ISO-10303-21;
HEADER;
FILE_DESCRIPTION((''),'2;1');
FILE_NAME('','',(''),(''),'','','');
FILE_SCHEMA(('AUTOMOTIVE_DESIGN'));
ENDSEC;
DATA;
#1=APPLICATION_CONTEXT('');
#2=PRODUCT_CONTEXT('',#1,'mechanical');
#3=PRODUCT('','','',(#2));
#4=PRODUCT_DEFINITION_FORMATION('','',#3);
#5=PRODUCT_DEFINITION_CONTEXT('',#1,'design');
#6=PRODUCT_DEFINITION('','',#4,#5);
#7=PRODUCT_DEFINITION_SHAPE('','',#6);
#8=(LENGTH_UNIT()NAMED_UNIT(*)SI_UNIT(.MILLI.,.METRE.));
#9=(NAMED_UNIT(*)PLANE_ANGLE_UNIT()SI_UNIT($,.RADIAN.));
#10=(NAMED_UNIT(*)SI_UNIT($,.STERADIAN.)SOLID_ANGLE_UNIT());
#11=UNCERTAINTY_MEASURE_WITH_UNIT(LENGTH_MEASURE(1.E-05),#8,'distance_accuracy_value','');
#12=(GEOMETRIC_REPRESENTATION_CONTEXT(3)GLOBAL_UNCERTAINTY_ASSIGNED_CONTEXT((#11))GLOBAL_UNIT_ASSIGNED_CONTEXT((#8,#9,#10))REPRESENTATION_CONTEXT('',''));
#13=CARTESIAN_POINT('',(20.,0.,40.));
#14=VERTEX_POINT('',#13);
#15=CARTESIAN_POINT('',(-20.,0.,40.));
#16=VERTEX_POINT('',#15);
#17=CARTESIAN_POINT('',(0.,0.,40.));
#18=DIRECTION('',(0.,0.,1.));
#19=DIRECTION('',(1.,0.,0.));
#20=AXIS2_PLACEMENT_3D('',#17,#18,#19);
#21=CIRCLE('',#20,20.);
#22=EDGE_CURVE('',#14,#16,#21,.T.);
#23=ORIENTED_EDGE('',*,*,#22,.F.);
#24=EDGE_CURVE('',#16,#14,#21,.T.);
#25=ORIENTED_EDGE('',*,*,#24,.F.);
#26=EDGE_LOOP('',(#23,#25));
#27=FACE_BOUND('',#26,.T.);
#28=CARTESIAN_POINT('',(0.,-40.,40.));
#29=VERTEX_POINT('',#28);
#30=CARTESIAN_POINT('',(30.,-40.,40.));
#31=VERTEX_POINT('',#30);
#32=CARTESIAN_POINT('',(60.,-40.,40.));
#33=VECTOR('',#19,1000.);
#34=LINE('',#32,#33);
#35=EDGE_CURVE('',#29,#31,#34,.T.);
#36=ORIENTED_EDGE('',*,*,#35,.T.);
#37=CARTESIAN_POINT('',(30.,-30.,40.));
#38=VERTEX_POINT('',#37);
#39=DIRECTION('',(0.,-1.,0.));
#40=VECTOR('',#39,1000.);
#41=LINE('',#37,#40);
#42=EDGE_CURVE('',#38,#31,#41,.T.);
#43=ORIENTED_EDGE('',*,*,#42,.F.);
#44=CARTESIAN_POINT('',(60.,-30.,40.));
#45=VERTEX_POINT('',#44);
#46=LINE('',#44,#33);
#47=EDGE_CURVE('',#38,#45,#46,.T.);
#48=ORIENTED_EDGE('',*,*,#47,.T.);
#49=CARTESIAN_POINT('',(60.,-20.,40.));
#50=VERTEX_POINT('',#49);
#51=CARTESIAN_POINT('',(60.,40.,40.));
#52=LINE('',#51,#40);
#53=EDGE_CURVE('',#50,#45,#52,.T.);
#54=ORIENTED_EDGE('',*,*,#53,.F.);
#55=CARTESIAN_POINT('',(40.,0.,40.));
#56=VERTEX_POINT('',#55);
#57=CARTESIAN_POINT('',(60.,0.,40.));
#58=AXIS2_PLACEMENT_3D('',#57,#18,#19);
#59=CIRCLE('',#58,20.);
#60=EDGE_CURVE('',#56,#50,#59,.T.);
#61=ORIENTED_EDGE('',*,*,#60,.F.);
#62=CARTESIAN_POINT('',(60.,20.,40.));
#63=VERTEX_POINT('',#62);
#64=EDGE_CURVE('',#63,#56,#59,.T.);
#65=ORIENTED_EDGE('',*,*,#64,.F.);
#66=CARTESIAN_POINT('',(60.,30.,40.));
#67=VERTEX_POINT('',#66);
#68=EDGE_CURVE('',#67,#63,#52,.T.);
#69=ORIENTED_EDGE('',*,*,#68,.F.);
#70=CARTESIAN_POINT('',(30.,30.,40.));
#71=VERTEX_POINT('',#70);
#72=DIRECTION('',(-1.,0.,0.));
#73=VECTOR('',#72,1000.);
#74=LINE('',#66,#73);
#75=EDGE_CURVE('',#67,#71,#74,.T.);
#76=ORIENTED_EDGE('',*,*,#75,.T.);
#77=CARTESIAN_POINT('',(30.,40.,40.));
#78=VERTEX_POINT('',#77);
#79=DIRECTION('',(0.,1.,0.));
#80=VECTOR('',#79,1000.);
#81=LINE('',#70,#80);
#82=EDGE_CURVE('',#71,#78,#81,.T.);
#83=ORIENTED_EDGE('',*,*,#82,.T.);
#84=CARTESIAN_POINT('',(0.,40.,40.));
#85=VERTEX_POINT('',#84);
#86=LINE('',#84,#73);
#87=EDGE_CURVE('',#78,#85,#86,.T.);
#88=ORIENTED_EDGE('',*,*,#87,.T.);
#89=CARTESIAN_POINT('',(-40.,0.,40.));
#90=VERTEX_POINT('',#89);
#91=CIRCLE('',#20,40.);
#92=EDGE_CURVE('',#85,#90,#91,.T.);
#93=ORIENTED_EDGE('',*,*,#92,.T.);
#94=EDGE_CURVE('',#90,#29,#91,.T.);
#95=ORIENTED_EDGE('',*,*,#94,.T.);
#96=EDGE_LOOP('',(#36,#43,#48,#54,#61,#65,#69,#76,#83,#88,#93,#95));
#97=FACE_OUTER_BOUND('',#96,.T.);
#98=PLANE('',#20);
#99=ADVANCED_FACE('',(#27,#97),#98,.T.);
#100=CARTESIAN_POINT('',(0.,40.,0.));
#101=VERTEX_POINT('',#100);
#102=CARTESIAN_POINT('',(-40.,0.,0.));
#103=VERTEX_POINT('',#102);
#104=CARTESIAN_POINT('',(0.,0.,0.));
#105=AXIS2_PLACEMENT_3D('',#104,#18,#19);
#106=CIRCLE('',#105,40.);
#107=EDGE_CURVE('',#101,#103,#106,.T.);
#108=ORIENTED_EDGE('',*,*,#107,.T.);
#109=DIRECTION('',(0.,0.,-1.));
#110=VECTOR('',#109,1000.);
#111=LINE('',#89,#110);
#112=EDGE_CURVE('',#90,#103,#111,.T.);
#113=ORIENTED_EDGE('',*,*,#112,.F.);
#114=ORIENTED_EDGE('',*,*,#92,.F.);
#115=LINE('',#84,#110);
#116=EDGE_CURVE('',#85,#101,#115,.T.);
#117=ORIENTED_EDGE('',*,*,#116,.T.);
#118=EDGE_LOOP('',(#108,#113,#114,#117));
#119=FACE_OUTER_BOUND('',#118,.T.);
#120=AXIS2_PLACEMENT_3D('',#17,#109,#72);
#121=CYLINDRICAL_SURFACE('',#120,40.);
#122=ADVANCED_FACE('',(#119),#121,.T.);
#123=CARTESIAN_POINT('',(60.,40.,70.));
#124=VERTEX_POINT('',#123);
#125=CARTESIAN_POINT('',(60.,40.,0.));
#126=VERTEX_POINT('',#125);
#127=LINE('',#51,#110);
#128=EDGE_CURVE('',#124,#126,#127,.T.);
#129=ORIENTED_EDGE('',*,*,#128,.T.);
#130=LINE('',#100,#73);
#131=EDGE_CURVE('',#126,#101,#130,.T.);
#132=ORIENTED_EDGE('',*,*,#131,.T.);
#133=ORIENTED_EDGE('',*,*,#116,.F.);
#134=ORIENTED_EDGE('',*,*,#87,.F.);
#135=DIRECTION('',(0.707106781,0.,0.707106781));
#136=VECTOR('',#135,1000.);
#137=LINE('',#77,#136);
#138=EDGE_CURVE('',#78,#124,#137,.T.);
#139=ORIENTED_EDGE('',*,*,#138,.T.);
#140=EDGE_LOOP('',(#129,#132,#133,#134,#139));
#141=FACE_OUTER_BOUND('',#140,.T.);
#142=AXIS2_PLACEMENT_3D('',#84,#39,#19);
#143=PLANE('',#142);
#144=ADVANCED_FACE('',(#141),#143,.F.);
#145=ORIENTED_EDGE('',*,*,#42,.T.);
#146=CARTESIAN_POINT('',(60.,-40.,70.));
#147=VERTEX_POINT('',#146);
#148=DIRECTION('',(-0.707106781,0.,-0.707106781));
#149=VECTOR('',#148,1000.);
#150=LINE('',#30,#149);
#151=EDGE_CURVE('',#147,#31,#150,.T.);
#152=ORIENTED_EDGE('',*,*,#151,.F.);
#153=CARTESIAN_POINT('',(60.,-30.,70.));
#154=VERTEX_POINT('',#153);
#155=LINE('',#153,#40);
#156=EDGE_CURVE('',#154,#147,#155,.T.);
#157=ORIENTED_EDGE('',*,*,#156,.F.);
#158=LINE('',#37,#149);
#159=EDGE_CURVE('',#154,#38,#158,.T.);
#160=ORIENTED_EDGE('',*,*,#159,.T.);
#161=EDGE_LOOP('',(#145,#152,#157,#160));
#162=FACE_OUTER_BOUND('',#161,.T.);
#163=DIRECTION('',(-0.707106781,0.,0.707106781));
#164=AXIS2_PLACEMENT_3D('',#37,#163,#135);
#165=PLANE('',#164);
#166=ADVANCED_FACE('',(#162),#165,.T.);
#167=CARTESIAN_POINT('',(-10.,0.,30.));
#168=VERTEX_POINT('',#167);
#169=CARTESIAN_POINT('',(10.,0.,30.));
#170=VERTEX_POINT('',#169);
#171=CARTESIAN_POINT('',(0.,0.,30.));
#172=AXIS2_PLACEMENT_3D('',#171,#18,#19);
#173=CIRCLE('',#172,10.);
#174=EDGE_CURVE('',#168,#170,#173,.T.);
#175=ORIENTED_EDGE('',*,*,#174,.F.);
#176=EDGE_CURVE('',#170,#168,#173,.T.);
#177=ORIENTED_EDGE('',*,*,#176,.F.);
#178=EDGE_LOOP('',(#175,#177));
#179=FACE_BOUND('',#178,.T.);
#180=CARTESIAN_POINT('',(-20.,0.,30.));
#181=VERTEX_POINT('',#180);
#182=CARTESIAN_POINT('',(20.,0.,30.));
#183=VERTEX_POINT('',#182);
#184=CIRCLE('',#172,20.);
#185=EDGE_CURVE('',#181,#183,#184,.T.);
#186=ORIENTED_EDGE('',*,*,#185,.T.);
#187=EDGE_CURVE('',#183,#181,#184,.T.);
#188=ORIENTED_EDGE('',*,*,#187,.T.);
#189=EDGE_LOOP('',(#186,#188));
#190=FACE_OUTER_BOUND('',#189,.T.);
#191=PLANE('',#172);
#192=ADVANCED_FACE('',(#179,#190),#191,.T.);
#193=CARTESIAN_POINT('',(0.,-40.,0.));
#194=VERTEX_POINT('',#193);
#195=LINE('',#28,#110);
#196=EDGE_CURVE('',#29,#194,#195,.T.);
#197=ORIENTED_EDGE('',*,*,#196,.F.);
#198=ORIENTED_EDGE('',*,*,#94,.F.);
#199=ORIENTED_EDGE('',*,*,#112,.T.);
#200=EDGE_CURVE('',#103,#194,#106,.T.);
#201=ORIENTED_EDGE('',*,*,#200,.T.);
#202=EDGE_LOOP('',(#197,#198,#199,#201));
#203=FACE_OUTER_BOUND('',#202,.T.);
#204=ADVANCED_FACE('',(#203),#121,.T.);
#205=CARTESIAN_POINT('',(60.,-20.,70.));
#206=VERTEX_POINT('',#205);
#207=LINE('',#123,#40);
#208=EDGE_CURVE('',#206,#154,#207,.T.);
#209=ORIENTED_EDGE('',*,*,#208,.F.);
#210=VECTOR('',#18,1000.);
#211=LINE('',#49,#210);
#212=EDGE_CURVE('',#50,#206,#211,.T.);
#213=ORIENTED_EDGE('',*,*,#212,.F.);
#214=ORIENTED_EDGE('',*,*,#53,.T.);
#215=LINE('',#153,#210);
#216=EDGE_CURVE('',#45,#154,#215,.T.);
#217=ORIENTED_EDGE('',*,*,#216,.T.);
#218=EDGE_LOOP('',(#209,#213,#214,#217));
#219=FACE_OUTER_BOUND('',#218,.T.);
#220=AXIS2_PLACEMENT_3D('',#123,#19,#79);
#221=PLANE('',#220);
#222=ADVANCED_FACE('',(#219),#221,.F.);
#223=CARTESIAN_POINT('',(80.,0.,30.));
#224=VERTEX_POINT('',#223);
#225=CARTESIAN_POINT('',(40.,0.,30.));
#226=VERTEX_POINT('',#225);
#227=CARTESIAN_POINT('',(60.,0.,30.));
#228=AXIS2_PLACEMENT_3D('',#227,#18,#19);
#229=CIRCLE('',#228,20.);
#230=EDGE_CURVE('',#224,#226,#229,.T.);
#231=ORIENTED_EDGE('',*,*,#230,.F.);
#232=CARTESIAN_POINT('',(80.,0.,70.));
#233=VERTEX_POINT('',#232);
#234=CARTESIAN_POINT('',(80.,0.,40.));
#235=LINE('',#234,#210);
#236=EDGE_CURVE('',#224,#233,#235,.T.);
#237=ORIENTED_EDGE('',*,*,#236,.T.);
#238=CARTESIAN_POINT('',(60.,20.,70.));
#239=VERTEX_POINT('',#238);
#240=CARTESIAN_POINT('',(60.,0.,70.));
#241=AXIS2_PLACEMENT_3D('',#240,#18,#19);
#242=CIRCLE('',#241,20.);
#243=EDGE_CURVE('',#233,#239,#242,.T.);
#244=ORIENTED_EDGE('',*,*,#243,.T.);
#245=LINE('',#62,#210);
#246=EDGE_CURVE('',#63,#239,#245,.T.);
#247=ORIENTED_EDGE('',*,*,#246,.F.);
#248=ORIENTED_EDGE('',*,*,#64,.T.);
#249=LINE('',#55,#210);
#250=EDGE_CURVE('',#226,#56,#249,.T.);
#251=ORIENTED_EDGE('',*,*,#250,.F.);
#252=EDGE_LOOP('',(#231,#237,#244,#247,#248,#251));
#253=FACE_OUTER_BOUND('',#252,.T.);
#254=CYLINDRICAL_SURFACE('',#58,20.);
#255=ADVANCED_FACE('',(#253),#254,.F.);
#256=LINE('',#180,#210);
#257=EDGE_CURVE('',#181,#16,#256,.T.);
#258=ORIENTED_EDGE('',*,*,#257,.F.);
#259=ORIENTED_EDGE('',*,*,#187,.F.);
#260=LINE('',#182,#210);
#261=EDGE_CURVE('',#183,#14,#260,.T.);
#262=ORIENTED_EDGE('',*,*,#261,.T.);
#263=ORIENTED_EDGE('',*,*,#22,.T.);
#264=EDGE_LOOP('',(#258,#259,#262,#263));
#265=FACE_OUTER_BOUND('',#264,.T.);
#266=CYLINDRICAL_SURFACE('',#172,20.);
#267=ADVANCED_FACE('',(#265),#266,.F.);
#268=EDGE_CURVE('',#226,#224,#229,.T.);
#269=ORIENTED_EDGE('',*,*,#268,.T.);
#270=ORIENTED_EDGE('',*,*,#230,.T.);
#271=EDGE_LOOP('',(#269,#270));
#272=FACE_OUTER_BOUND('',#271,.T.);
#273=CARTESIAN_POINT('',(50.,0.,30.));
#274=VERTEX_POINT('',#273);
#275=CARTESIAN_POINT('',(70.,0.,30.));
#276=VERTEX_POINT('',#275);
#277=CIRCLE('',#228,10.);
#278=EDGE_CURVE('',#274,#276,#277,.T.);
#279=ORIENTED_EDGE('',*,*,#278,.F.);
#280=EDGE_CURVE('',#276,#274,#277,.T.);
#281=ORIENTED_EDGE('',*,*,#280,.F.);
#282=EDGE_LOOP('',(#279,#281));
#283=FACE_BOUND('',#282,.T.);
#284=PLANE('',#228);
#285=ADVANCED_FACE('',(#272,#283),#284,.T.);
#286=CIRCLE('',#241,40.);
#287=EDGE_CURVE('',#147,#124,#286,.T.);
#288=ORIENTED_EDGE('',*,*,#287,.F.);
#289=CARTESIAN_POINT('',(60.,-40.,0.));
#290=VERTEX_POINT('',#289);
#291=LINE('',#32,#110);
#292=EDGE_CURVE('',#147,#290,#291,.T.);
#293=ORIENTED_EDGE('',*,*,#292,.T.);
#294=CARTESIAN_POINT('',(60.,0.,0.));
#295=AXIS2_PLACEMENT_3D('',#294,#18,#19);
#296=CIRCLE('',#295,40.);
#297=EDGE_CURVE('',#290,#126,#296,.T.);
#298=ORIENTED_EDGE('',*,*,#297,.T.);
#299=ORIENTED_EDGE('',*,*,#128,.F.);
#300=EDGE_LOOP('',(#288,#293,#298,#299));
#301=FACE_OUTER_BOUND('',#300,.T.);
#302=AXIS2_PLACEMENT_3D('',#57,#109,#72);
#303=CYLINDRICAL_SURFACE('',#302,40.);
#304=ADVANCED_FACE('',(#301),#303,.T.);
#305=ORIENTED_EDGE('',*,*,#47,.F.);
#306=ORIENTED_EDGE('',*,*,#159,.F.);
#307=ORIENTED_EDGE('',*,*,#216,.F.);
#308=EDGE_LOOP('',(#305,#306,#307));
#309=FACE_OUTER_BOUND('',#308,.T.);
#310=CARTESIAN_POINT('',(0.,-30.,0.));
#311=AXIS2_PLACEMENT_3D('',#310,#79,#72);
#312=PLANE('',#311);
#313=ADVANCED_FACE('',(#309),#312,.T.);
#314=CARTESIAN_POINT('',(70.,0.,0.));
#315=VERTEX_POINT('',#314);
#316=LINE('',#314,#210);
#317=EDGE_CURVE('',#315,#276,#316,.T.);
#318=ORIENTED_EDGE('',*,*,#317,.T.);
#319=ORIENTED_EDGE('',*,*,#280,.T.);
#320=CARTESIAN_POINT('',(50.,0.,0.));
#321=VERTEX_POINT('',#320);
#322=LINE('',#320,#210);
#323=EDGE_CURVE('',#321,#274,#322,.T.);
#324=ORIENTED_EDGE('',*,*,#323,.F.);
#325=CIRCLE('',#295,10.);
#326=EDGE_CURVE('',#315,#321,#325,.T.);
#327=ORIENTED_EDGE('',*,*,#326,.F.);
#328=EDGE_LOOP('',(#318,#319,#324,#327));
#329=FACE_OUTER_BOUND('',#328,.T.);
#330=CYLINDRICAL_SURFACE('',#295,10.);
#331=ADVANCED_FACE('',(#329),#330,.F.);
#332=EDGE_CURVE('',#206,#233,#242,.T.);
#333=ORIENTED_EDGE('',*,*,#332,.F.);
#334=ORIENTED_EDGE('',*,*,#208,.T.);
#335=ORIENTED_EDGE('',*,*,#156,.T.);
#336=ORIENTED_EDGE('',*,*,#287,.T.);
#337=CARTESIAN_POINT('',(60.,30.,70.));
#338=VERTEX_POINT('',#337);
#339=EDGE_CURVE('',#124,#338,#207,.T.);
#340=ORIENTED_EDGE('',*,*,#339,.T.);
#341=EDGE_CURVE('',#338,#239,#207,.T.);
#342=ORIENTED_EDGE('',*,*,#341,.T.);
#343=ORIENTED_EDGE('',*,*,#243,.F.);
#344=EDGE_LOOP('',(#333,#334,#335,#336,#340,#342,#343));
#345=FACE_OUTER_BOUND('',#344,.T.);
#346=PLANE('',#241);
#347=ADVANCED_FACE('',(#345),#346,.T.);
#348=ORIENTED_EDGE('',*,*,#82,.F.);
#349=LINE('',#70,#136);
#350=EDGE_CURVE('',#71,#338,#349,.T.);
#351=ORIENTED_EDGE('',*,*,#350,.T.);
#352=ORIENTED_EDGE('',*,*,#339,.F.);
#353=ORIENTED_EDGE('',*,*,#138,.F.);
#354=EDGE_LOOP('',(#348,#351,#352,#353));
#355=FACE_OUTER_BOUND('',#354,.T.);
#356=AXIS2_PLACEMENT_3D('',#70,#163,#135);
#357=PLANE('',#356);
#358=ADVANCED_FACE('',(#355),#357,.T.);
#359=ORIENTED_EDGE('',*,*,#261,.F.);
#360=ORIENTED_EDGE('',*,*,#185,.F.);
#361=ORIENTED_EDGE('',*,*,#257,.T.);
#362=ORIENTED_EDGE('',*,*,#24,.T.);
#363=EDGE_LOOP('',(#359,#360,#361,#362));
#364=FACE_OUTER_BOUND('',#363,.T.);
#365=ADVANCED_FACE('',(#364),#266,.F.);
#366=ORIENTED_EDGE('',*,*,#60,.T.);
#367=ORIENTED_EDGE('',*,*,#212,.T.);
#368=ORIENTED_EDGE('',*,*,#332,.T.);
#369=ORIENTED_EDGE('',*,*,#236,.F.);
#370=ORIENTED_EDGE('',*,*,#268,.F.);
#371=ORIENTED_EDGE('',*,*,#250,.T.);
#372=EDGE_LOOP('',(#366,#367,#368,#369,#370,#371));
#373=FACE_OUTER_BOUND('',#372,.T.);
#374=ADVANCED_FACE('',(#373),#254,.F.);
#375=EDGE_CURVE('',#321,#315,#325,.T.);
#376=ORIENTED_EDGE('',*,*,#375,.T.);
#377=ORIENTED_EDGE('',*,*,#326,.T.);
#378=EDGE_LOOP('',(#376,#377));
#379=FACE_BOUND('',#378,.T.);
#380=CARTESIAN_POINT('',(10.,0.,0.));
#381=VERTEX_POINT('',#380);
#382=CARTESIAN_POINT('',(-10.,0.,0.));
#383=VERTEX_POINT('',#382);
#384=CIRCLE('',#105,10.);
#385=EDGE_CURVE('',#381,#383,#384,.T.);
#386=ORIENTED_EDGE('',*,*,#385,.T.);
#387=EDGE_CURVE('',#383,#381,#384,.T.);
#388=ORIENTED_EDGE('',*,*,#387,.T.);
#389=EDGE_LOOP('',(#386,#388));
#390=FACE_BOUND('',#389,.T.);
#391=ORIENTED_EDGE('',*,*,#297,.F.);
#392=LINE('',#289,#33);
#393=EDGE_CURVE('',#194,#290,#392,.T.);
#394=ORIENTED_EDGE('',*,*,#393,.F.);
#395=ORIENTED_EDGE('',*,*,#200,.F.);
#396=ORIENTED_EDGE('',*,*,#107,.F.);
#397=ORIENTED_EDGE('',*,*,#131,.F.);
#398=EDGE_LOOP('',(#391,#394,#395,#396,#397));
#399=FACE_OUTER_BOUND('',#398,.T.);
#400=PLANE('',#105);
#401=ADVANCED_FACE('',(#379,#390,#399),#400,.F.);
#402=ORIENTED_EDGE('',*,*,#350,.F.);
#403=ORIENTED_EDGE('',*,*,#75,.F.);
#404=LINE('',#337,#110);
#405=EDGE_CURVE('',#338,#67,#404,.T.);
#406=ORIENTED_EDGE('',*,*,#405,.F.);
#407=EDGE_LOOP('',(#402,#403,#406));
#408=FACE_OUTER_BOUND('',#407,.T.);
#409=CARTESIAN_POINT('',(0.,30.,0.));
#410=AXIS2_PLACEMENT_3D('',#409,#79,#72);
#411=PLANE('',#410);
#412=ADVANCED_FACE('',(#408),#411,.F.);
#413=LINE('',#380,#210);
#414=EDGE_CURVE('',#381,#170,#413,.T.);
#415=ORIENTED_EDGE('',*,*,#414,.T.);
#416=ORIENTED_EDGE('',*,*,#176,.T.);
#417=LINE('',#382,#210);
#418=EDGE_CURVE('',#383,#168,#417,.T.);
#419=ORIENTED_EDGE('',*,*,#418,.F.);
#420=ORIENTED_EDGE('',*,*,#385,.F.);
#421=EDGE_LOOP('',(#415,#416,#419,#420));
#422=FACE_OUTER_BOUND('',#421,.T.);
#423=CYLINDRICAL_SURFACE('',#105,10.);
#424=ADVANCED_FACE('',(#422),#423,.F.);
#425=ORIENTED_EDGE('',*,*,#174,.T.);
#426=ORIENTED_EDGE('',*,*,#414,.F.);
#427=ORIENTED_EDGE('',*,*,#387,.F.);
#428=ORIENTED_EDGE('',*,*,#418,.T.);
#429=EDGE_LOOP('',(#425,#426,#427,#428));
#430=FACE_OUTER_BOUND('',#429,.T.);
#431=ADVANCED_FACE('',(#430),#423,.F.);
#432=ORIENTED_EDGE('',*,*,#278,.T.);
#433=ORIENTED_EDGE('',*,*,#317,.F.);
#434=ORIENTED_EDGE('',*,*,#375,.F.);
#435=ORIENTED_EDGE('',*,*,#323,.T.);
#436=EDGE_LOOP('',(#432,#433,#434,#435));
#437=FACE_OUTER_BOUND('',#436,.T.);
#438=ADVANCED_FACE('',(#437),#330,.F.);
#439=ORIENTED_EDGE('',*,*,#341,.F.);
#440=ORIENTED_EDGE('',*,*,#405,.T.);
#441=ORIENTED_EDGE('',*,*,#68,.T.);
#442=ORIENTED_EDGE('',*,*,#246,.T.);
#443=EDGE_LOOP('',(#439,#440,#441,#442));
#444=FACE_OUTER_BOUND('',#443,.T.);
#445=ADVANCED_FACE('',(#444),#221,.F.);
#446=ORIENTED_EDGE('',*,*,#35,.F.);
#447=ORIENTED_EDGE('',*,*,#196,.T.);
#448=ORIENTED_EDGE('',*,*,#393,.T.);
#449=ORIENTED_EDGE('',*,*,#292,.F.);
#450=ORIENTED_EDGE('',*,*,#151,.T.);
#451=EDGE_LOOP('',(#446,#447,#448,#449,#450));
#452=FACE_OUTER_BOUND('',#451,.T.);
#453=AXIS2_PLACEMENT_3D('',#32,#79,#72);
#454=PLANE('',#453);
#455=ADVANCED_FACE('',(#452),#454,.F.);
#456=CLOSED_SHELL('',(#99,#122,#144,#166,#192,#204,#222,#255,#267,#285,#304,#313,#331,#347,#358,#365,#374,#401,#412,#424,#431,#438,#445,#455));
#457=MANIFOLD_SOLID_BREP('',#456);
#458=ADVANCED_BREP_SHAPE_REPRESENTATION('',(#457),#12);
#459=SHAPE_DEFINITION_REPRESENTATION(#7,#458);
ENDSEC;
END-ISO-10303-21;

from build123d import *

# Parameters (mm, degrees)
BASE_BLOCK_80X80X40_DEPTH = 40
COUNTERBORE_1_SKETCH_R    = 20
COUNTERBORE_1_40X10_DEPTH = 10
BORE_1_SKETCH_R           = 10
BORE_1_20_DEPTH           = 30
SIDE_BOSS_DEPTH           = 30
SIDE_BOSS_TRIM_CUT_DEPTH  = 30
COUNTERBORE_2_SKETCH_R    = 20
COUNTERBORE_2_40X10_DEPTH = 10
BORE_2_SKETCH_R           = 10
BORE_2_20_DEPTH           = 30
GUSSET_1_DEPTH            = 10
GUSSET_2_DEPTH            = 10


with BuildPart() as part:
    # Base Block Sketch → Base Block 80x80x40 (new body)
    with BuildSketch(Plane.XY):
        with BuildLine():
            Line((0, 40), (60, 40))
            ThreePointArc((60, 40), (100, 0), (60, -40))
            Line((60, -40), (0, -40))
            ThreePointArc((0, -40), (-40, 0), (0, 40))
        make_face()
    extrude(amount=BASE_BLOCK_80X80X40_DEPTH)

    # Counterbore 1 Sketch → Counterbore 1 Ø40x10 (cut)
    with BuildSketch(Plane.XY.offset(40)):
        Circle(COUNTERBORE_1_SKETCH_R)
    extrude(amount=-COUNTERBORE_1_40X10_DEPTH, mode=Mode.SUBTRACT)

    # Bore 1 Sketch → Bore 1 Ø20 (cut)
    with BuildSketch(Plane.XY.offset(30)):
        Circle(BORE_1_SKETCH_R)
    extrude(amount=-BORE_1_20_DEPTH, mode=Mode.SUBTRACT)

    # Side Boss Sketch → Side Boss (add)
    with BuildSketch(Plane.XY.offset(40)):
        with BuildLine():
            Line((60, 40), (60, -40))
            ThreePointArc((60, -40), (100, 0), (60, 40))
        make_face()
    extrude(amount=SIDE_BOSS_DEPTH)

    # Side Boss Trim Sketch → Side Boss Trim Cut (cut)
    with BuildSketch(Plane.XY.offset(70)):
        with BuildLine():
            Line((60, 20), (60, -20))
            ThreePointArc((60, -20), (80, 0), (60, 20))
        make_face()
    extrude(amount=-SIDE_BOSS_TRIM_CUT_DEPTH, mode=Mode.SUBTRACT)

    # Counterbore 2 Sketch → Counterbore 2 Ø40x10 (cut)
    with BuildSketch(Plane.XY.offset(40)):
        with Locations((60, 0)):
            Circle(COUNTERBORE_2_SKETCH_R)
    extrude(amount=-COUNTERBORE_2_40X10_DEPTH, mode=Mode.SUBTRACT)

    # Bore 2 Sketch → Bore 2 Ø20 (cut)
    with BuildSketch(Plane.XY.offset(30)):
        with Locations((60, 0)):
            Circle(BORE_2_SKETCH_R)
    extrude(amount=-BORE_2_20_DEPTH, mode=Mode.SUBTRACT)

    # Gusset 1 Sketch → Gusset 1 (add)
    with BuildSketch(Plane.XZ.offset(40)):
        Polygon((60, 70), (60, 40), (30, 40), align=None)
    extrude(amount=-GUSSET_1_DEPTH)

    # Gusset 2 Sketch → Gusset 2 (add)
    with BuildSketch(Plane(origin=(0, 40, 0), x_dir=(1, 0, 0), z_dir=(0, 1, 0))):
        Polygon((60, -70), (60, -40), (30, -40), align=None)
    extrude(amount=-GUSSET_2_DEPTH)


solid = part.part
